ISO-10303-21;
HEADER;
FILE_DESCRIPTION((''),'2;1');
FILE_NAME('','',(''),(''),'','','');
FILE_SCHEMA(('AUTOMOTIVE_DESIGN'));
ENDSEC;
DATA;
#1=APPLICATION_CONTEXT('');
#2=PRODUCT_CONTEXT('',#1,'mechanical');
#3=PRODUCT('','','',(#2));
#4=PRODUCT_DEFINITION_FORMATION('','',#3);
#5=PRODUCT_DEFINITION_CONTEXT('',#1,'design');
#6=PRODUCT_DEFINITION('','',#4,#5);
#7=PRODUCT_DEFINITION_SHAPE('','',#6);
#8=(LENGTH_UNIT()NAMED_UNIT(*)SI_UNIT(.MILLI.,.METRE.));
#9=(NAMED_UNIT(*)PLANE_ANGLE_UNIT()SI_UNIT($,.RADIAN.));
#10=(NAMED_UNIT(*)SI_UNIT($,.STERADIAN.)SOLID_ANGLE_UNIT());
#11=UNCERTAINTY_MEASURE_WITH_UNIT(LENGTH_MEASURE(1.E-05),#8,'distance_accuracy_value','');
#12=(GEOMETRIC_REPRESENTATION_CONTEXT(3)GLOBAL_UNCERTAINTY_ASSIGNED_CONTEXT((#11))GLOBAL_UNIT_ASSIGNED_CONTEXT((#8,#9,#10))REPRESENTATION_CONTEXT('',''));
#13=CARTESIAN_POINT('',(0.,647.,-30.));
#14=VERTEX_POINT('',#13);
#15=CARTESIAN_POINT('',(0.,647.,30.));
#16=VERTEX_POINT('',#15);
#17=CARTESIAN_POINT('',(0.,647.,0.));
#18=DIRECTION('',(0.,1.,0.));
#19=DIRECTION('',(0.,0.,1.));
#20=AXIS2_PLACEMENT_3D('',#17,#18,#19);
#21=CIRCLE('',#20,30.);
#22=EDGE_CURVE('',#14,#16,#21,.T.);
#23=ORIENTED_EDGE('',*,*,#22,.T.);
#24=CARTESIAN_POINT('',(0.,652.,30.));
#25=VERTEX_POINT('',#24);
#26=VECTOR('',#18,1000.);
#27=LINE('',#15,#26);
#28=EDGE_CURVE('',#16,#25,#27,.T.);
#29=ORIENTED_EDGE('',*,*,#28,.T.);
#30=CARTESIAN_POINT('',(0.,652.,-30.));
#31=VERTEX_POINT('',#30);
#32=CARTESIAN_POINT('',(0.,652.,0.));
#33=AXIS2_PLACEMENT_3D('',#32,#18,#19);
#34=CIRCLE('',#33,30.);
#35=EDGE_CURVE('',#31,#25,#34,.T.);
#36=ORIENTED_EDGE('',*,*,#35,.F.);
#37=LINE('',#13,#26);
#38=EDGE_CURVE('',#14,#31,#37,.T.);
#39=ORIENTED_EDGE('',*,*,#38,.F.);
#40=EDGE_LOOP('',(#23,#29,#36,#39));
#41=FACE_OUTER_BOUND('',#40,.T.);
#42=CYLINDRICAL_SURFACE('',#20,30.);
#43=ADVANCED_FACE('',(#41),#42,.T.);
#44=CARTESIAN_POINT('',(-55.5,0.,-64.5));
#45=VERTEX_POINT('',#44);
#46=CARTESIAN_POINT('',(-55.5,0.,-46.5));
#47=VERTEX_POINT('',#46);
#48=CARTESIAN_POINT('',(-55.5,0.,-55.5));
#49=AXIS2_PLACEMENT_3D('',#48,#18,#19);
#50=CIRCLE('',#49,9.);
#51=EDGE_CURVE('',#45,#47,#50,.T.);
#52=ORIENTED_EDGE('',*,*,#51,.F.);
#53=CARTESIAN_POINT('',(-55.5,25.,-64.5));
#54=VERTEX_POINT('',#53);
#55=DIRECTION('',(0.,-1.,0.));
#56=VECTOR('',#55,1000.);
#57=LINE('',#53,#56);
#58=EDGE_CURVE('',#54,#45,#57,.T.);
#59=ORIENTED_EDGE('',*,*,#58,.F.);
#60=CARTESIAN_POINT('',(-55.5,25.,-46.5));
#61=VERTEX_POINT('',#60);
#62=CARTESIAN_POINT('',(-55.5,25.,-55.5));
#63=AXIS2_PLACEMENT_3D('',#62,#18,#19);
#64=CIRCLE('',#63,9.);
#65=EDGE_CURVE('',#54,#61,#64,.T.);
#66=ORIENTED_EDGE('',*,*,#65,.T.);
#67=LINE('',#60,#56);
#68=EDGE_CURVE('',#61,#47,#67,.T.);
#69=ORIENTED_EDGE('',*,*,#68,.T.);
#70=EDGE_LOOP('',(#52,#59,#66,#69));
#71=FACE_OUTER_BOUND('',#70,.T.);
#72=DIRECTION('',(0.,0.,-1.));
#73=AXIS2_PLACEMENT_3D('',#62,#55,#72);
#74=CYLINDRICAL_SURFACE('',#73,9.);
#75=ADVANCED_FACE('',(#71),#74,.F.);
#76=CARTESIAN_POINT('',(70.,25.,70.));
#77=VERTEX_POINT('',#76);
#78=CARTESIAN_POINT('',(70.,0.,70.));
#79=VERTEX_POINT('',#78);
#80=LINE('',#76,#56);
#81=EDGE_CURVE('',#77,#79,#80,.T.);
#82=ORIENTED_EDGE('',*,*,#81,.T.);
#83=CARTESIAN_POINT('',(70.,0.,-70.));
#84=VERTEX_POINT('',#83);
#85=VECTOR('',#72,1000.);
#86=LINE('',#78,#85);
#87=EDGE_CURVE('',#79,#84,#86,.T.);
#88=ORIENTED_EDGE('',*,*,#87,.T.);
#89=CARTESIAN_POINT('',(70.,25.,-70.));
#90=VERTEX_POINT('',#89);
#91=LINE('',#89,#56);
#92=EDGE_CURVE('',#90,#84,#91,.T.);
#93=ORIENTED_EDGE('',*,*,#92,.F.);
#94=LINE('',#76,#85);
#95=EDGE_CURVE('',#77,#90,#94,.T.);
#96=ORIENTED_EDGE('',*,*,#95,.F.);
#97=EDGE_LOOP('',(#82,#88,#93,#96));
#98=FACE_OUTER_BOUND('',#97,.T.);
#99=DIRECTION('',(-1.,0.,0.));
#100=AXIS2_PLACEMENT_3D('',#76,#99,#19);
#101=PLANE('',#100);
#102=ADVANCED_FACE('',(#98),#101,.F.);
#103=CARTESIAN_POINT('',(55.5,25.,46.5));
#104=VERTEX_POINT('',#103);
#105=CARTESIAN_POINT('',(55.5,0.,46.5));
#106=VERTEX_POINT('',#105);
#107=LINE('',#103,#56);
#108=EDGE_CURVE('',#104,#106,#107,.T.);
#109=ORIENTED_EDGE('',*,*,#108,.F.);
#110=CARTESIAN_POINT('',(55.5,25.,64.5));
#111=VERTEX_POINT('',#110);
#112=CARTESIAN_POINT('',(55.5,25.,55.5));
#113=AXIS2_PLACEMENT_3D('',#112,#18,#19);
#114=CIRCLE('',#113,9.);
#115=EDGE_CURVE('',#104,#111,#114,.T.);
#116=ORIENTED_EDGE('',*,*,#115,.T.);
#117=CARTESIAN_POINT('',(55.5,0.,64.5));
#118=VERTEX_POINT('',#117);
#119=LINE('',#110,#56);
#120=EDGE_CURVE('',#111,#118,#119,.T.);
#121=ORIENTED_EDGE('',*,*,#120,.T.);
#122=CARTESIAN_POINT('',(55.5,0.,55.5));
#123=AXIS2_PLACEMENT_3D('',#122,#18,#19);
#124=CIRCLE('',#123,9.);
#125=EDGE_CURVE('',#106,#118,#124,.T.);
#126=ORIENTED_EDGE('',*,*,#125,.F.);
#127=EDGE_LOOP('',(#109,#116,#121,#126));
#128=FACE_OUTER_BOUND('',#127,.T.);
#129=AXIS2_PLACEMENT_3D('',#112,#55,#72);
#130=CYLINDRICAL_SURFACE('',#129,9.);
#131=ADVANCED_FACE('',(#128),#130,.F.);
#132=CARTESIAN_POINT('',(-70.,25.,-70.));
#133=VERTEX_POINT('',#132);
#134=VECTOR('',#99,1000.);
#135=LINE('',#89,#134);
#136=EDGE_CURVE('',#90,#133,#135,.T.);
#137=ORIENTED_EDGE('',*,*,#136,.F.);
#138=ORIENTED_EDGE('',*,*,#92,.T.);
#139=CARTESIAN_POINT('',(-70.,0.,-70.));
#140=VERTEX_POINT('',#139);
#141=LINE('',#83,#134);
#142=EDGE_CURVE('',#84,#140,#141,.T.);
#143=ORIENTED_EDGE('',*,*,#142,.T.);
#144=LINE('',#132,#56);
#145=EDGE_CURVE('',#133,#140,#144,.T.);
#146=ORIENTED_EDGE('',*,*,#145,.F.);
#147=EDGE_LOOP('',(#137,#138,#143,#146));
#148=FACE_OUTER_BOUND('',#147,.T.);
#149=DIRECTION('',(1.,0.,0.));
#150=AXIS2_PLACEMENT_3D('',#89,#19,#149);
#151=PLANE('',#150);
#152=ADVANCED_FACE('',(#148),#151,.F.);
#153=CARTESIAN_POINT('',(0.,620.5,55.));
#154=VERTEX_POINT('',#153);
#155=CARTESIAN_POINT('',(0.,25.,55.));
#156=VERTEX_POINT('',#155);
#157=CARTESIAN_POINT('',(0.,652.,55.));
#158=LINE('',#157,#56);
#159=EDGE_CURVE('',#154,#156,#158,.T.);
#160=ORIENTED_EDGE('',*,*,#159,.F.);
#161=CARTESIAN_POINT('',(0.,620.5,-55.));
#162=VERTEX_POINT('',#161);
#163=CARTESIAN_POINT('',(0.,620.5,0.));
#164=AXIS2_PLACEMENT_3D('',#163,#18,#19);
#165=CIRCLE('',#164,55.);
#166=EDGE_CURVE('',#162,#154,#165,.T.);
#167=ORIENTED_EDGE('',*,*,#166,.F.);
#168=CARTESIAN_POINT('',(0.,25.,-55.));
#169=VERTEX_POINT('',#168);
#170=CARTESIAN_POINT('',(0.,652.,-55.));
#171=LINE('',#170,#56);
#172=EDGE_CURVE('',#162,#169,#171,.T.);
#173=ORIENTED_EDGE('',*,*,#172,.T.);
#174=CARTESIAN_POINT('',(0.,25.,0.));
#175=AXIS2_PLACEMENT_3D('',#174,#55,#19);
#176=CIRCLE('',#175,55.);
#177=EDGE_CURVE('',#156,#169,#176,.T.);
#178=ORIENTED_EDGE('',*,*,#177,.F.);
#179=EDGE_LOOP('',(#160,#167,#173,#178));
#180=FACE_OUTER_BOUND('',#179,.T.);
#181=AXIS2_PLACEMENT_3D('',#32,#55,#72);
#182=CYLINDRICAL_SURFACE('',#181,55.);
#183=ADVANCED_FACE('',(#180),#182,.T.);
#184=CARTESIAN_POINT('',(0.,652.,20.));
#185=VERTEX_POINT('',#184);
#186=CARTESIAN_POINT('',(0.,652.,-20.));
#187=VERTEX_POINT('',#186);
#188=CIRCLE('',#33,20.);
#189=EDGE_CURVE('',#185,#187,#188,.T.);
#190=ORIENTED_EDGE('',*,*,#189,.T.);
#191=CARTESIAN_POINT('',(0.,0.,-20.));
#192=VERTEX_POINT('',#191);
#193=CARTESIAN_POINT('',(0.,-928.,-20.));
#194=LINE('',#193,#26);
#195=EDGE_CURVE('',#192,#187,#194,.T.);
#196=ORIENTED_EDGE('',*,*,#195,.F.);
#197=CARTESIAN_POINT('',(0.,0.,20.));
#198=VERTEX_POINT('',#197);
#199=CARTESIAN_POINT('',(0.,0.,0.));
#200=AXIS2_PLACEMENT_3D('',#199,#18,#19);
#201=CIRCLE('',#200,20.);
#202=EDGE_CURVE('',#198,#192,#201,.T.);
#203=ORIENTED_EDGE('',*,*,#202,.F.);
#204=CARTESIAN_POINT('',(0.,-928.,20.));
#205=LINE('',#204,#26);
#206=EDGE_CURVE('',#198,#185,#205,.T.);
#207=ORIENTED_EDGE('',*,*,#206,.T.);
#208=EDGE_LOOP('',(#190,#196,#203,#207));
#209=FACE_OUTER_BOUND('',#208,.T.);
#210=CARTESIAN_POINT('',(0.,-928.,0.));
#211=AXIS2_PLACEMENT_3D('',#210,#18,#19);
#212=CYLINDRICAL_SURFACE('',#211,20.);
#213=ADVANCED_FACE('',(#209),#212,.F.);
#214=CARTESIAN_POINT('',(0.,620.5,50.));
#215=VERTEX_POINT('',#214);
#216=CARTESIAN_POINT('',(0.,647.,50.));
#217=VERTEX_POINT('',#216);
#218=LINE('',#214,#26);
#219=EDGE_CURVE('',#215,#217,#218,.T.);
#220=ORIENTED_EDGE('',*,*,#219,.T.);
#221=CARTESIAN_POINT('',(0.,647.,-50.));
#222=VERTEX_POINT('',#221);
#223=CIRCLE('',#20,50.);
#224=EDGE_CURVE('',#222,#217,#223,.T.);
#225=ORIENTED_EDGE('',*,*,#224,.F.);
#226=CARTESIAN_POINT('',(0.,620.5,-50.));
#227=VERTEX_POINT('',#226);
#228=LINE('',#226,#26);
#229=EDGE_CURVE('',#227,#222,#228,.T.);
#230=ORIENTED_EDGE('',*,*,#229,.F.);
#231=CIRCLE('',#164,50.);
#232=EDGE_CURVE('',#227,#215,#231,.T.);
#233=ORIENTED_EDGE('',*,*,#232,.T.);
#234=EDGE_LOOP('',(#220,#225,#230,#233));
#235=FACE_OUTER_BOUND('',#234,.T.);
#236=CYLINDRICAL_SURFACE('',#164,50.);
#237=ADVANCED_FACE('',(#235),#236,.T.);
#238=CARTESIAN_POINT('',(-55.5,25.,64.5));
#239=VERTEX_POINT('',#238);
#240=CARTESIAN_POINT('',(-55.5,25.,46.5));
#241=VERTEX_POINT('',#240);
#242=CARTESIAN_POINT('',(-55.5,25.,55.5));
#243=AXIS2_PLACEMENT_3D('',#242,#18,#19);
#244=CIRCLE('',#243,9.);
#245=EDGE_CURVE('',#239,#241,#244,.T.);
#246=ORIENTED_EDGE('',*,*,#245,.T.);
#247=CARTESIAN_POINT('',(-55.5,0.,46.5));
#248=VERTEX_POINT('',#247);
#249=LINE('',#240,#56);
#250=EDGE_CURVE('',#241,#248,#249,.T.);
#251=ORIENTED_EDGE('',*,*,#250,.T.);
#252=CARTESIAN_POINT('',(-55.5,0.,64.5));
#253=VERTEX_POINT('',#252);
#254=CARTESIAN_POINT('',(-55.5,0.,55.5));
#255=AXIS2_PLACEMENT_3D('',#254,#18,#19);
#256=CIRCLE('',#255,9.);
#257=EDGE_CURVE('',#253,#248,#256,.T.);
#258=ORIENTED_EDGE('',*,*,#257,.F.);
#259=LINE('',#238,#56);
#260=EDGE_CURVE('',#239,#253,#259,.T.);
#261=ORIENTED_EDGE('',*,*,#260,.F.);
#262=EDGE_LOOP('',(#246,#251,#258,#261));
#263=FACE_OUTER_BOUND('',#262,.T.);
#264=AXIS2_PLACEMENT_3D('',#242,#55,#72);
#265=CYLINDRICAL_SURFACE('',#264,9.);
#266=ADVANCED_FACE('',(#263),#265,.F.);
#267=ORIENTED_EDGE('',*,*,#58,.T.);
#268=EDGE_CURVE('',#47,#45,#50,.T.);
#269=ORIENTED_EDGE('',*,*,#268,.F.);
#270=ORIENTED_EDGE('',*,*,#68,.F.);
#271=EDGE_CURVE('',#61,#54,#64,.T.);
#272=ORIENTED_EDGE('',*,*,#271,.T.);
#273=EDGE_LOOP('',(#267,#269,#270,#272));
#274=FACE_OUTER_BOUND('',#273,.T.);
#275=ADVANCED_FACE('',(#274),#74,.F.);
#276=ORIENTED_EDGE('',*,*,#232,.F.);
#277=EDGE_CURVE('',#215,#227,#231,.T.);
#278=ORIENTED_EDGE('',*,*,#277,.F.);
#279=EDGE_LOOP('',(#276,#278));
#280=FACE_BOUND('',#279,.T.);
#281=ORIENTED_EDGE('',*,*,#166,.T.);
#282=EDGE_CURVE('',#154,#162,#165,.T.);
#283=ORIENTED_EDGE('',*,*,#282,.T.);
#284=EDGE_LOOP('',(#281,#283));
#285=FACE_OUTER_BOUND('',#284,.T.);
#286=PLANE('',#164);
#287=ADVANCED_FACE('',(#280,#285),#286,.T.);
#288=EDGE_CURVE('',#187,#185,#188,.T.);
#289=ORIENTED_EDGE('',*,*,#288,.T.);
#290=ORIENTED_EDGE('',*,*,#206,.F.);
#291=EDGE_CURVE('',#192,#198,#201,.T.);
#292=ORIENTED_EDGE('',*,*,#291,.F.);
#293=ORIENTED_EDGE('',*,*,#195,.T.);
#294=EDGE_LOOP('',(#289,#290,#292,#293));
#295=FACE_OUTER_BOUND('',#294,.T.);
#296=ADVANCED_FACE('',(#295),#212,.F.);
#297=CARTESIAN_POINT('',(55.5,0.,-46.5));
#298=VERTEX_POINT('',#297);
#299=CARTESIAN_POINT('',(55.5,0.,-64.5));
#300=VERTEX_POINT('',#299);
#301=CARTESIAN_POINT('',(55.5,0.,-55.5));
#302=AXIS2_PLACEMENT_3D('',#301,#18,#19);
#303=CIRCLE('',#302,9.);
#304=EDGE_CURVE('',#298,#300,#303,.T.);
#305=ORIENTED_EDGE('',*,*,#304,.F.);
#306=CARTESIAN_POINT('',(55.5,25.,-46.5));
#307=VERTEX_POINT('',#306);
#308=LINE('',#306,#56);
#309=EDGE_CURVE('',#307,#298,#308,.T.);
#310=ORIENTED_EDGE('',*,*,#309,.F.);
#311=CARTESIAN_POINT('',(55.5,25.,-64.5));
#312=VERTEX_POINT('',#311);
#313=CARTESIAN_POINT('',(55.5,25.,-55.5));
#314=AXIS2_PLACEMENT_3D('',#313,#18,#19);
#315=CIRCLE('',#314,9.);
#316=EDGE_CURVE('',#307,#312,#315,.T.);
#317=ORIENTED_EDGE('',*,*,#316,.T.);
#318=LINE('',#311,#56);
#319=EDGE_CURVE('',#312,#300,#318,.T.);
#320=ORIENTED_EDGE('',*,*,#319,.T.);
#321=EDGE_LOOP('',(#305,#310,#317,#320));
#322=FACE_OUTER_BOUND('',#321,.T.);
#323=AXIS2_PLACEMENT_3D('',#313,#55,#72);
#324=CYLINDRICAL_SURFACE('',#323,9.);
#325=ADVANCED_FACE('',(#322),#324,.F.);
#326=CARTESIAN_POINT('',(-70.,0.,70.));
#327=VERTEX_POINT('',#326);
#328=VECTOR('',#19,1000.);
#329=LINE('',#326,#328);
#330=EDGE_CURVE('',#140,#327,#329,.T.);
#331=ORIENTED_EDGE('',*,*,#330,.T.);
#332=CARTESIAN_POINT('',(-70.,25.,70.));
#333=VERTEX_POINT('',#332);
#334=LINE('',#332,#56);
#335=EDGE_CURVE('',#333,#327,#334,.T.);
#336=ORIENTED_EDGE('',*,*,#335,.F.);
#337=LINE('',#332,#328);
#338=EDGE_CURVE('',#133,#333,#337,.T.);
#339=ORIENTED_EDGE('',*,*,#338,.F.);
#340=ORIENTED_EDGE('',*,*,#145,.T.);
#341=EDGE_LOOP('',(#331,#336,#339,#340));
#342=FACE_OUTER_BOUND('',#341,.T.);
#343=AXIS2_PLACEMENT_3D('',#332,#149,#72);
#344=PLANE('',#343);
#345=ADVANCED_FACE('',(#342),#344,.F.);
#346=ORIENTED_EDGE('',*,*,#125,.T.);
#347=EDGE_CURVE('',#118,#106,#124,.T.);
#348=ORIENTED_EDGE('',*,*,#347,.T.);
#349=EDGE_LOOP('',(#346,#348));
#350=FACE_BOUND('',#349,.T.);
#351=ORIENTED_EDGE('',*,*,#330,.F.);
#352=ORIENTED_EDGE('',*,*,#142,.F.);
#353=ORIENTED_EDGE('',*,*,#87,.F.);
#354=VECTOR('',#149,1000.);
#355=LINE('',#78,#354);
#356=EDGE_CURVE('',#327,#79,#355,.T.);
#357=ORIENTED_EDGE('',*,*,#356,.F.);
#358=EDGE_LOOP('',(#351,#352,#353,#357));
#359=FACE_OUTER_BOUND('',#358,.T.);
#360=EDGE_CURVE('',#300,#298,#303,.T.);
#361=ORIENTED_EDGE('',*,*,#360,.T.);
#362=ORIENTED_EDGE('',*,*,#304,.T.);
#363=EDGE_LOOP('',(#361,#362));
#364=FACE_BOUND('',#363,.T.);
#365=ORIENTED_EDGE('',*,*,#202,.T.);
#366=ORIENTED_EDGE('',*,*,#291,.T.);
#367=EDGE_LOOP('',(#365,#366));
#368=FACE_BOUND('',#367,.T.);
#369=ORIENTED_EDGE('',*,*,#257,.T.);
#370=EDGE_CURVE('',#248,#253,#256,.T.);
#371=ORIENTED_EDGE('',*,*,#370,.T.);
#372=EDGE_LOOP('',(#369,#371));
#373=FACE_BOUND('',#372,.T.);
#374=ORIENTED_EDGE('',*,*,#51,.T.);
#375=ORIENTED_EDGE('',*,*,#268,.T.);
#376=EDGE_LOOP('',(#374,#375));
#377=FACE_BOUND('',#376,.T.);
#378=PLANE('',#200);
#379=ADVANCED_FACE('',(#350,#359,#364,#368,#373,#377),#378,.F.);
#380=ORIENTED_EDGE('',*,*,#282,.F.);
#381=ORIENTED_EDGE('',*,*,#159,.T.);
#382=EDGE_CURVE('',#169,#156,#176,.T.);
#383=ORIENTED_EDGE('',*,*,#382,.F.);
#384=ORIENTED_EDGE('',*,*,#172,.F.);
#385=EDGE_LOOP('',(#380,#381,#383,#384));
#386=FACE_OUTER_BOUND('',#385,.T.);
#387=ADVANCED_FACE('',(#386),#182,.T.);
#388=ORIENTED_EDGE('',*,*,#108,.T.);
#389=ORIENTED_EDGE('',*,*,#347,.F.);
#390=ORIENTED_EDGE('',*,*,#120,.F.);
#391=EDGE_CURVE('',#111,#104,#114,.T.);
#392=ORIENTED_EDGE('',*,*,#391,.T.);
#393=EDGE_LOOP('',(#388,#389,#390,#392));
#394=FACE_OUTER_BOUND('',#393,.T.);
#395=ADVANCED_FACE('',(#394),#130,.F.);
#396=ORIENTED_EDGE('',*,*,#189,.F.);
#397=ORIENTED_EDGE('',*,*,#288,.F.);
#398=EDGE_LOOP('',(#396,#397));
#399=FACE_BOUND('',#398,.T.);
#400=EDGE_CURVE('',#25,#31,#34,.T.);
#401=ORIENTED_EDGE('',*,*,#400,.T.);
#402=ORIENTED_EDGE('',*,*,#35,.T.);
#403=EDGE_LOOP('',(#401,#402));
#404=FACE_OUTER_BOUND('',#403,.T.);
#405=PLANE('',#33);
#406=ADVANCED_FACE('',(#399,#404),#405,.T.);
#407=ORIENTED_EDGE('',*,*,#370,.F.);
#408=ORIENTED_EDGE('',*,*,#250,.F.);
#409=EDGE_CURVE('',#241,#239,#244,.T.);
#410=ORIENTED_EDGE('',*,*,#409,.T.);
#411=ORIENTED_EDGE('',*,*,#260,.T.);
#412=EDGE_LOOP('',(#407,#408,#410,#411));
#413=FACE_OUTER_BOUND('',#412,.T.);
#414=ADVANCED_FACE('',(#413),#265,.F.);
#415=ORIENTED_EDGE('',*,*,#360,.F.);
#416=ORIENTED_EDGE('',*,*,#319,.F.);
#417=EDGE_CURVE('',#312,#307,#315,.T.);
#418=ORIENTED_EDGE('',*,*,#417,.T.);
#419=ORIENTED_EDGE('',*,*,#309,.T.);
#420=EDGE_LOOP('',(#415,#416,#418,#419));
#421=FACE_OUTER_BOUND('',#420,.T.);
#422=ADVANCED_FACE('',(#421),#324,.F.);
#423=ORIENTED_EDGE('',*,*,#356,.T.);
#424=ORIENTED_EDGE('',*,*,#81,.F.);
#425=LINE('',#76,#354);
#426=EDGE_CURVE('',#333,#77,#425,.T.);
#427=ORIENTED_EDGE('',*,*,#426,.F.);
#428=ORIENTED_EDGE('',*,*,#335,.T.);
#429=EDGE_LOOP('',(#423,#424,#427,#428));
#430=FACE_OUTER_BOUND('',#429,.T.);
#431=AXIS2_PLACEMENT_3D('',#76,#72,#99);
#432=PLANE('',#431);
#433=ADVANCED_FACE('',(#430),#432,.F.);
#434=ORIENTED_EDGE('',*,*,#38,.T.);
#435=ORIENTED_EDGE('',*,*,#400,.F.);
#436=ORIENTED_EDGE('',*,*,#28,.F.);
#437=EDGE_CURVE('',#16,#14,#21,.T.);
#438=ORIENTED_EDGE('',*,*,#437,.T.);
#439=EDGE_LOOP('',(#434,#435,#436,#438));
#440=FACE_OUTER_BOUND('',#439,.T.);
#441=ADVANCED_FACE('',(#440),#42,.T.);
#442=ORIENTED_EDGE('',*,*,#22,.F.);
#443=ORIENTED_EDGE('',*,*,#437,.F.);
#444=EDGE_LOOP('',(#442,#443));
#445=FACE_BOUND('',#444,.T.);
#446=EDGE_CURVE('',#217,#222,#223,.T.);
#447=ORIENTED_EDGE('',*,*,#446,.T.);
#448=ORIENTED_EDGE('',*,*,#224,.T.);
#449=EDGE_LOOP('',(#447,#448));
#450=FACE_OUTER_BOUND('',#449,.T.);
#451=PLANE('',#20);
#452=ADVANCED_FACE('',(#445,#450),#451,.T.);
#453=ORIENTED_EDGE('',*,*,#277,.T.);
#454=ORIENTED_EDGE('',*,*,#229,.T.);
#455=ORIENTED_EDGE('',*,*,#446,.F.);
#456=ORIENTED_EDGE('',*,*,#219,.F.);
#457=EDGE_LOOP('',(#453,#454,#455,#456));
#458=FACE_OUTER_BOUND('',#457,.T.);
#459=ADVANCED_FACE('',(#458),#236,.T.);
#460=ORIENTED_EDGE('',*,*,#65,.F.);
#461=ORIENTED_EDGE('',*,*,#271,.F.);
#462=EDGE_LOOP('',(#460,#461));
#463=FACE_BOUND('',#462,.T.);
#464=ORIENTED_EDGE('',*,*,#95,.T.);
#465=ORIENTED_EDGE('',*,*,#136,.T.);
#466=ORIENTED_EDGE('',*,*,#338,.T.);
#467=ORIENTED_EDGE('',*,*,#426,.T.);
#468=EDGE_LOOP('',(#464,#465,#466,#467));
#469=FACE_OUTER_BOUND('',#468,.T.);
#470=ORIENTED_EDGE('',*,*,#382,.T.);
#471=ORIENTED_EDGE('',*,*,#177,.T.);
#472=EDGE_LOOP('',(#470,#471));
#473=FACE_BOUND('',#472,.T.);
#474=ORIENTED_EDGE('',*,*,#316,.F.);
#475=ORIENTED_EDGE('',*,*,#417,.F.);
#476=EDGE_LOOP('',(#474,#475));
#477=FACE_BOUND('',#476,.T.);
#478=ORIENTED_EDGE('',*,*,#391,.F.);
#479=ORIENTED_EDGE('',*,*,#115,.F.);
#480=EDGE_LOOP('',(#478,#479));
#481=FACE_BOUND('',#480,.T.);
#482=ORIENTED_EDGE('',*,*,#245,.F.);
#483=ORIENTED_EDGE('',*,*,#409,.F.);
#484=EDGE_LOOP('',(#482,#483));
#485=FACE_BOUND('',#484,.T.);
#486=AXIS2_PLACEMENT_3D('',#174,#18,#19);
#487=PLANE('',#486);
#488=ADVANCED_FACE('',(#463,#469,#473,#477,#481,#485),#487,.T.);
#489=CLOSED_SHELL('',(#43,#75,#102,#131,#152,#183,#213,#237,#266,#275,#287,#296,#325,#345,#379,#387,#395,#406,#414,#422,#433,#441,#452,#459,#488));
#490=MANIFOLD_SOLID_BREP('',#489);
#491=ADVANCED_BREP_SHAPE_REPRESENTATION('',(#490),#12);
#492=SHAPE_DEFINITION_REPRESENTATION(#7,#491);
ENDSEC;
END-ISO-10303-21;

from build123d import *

# Parameters (mm, degrees)
SKETCH1_W           = 140
SKETCH1_H           = 140
SKETCH1_R           = 9
BOSS_EXTRUDE1_DEPTH = 25
SKETCH2_R           = 55
BOSS_EXTRUDE2_DEPTH = 652
SKETCH3_R           = 20
CUT_EXTRUDE1_DEPTH  = 1580
SKETCH4_OUTSIDE_W   = 278.28
SKETCH4_OUTSIDE_H   = 278.28
SKETCH4_OUTSIDE_R   = 30
CUT_EXTRUDE2_DEPTH  = 5
SKETCH6_OUTSIDE_W   = 278.28
SKETCH6_OUTSIDE_H   = 278.28
SKETCH6_OUTSIDE_R   = 50
CUT_EXTRUDE3_DEPTH  = 31.5


with BuildPart() as part:
    # Sketch1 → Boss-Extrude1 (new body)
    with BuildSketch(Plane(origin=(0, 0, 0), x_dir=(1, 0, 0), z_dir=(0, 1, 0))):
        Rectangle(SKETCH1_W, SKETCH1_H)
        with Locations(Location((-55.5, 55.5, 0), (0, 0, 270))):
            Circle(SKETCH1_R, mode=Mode.SUBTRACT)
        with Locations(Location((55.5, 55.5, 0), (0, 0, 270))):
            Circle(SKETCH1_R, mode=Mode.SUBTRACT)
        with Locations(Location((55.5, -55.5, 0), (0, 0, 270))):
            Circle(SKETCH1_R, mode=Mode.SUBTRACT)
        with Locations(Location((-55.5, -55.5, 0), (0, 0, 270))):
            Circle(SKETCH1_R, mode=Mode.SUBTRACT)
    extrude(amount=BOSS_EXTRUDE1_DEPTH)

    # Sketch2 → Boss-Extrude2 (add)
    with BuildSketch(Plane(origin=(0, 0, 0), x_dir=(1, 0, 0), z_dir=(0, 1, 0))):
        with Locations(Location((0, 0, 0), (0, 0, 270))):
            Circle(SKETCH2_R)
    extrude(amount=BOSS_EXTRUDE2_DEPTH)

    # Sketch3 → Cut-Extrude1 (cut)
    with BuildSketch(Plane(origin=(0, 652, 0), x_dir=(1, 0, 0), z_dir=(0, 1, 0))):
        with Locations(Location((0, 0, 0), (0, 0, 270))):
            Circle(SKETCH3_R)
    extrude(amount=-CUT_EXTRUDE1_DEPTH, mode=Mode.SUBTRACT)

    # Sketch4 outside → Cut-Extrude2 (cut)
    with BuildSketch(Plane(origin=(0, 652, 0), x_dir=(1, 0, 0), z_dir=(0, 1, 0))):
        Rectangle(SKETCH4_OUTSIDE_W, SKETCH4_OUTSIDE_H)
        with Locations(Location((0, 0, 0), (0, 0, 270))):
            Circle(SKETCH4_OUTSIDE_R, mode=Mode.SUBTRACT)
    extrude(amount=-CUT_EXTRUDE2_DEPTH, mode=Mode.SUBTRACT)

    # Sketch6 outside → Cut-Extrude3 (cut)
    with BuildSketch(Plane(origin=(0, 652, 0), x_dir=(1, 0, 0), z_dir=(0, 1, 0))):
        Rectangle(SKETCH6_OUTSIDE_W, SKETCH6_OUTSIDE_H)
        with Locations(Location((0, 0, 0), (0, 0, 270))):
            Circle(SKETCH6_OUTSIDE_R, mode=Mode.SUBTRACT)
    extrude(amount=-CUT_EXTRUDE3_DEPTH, mode=Mode.SUBTRACT)


solid = part.part
